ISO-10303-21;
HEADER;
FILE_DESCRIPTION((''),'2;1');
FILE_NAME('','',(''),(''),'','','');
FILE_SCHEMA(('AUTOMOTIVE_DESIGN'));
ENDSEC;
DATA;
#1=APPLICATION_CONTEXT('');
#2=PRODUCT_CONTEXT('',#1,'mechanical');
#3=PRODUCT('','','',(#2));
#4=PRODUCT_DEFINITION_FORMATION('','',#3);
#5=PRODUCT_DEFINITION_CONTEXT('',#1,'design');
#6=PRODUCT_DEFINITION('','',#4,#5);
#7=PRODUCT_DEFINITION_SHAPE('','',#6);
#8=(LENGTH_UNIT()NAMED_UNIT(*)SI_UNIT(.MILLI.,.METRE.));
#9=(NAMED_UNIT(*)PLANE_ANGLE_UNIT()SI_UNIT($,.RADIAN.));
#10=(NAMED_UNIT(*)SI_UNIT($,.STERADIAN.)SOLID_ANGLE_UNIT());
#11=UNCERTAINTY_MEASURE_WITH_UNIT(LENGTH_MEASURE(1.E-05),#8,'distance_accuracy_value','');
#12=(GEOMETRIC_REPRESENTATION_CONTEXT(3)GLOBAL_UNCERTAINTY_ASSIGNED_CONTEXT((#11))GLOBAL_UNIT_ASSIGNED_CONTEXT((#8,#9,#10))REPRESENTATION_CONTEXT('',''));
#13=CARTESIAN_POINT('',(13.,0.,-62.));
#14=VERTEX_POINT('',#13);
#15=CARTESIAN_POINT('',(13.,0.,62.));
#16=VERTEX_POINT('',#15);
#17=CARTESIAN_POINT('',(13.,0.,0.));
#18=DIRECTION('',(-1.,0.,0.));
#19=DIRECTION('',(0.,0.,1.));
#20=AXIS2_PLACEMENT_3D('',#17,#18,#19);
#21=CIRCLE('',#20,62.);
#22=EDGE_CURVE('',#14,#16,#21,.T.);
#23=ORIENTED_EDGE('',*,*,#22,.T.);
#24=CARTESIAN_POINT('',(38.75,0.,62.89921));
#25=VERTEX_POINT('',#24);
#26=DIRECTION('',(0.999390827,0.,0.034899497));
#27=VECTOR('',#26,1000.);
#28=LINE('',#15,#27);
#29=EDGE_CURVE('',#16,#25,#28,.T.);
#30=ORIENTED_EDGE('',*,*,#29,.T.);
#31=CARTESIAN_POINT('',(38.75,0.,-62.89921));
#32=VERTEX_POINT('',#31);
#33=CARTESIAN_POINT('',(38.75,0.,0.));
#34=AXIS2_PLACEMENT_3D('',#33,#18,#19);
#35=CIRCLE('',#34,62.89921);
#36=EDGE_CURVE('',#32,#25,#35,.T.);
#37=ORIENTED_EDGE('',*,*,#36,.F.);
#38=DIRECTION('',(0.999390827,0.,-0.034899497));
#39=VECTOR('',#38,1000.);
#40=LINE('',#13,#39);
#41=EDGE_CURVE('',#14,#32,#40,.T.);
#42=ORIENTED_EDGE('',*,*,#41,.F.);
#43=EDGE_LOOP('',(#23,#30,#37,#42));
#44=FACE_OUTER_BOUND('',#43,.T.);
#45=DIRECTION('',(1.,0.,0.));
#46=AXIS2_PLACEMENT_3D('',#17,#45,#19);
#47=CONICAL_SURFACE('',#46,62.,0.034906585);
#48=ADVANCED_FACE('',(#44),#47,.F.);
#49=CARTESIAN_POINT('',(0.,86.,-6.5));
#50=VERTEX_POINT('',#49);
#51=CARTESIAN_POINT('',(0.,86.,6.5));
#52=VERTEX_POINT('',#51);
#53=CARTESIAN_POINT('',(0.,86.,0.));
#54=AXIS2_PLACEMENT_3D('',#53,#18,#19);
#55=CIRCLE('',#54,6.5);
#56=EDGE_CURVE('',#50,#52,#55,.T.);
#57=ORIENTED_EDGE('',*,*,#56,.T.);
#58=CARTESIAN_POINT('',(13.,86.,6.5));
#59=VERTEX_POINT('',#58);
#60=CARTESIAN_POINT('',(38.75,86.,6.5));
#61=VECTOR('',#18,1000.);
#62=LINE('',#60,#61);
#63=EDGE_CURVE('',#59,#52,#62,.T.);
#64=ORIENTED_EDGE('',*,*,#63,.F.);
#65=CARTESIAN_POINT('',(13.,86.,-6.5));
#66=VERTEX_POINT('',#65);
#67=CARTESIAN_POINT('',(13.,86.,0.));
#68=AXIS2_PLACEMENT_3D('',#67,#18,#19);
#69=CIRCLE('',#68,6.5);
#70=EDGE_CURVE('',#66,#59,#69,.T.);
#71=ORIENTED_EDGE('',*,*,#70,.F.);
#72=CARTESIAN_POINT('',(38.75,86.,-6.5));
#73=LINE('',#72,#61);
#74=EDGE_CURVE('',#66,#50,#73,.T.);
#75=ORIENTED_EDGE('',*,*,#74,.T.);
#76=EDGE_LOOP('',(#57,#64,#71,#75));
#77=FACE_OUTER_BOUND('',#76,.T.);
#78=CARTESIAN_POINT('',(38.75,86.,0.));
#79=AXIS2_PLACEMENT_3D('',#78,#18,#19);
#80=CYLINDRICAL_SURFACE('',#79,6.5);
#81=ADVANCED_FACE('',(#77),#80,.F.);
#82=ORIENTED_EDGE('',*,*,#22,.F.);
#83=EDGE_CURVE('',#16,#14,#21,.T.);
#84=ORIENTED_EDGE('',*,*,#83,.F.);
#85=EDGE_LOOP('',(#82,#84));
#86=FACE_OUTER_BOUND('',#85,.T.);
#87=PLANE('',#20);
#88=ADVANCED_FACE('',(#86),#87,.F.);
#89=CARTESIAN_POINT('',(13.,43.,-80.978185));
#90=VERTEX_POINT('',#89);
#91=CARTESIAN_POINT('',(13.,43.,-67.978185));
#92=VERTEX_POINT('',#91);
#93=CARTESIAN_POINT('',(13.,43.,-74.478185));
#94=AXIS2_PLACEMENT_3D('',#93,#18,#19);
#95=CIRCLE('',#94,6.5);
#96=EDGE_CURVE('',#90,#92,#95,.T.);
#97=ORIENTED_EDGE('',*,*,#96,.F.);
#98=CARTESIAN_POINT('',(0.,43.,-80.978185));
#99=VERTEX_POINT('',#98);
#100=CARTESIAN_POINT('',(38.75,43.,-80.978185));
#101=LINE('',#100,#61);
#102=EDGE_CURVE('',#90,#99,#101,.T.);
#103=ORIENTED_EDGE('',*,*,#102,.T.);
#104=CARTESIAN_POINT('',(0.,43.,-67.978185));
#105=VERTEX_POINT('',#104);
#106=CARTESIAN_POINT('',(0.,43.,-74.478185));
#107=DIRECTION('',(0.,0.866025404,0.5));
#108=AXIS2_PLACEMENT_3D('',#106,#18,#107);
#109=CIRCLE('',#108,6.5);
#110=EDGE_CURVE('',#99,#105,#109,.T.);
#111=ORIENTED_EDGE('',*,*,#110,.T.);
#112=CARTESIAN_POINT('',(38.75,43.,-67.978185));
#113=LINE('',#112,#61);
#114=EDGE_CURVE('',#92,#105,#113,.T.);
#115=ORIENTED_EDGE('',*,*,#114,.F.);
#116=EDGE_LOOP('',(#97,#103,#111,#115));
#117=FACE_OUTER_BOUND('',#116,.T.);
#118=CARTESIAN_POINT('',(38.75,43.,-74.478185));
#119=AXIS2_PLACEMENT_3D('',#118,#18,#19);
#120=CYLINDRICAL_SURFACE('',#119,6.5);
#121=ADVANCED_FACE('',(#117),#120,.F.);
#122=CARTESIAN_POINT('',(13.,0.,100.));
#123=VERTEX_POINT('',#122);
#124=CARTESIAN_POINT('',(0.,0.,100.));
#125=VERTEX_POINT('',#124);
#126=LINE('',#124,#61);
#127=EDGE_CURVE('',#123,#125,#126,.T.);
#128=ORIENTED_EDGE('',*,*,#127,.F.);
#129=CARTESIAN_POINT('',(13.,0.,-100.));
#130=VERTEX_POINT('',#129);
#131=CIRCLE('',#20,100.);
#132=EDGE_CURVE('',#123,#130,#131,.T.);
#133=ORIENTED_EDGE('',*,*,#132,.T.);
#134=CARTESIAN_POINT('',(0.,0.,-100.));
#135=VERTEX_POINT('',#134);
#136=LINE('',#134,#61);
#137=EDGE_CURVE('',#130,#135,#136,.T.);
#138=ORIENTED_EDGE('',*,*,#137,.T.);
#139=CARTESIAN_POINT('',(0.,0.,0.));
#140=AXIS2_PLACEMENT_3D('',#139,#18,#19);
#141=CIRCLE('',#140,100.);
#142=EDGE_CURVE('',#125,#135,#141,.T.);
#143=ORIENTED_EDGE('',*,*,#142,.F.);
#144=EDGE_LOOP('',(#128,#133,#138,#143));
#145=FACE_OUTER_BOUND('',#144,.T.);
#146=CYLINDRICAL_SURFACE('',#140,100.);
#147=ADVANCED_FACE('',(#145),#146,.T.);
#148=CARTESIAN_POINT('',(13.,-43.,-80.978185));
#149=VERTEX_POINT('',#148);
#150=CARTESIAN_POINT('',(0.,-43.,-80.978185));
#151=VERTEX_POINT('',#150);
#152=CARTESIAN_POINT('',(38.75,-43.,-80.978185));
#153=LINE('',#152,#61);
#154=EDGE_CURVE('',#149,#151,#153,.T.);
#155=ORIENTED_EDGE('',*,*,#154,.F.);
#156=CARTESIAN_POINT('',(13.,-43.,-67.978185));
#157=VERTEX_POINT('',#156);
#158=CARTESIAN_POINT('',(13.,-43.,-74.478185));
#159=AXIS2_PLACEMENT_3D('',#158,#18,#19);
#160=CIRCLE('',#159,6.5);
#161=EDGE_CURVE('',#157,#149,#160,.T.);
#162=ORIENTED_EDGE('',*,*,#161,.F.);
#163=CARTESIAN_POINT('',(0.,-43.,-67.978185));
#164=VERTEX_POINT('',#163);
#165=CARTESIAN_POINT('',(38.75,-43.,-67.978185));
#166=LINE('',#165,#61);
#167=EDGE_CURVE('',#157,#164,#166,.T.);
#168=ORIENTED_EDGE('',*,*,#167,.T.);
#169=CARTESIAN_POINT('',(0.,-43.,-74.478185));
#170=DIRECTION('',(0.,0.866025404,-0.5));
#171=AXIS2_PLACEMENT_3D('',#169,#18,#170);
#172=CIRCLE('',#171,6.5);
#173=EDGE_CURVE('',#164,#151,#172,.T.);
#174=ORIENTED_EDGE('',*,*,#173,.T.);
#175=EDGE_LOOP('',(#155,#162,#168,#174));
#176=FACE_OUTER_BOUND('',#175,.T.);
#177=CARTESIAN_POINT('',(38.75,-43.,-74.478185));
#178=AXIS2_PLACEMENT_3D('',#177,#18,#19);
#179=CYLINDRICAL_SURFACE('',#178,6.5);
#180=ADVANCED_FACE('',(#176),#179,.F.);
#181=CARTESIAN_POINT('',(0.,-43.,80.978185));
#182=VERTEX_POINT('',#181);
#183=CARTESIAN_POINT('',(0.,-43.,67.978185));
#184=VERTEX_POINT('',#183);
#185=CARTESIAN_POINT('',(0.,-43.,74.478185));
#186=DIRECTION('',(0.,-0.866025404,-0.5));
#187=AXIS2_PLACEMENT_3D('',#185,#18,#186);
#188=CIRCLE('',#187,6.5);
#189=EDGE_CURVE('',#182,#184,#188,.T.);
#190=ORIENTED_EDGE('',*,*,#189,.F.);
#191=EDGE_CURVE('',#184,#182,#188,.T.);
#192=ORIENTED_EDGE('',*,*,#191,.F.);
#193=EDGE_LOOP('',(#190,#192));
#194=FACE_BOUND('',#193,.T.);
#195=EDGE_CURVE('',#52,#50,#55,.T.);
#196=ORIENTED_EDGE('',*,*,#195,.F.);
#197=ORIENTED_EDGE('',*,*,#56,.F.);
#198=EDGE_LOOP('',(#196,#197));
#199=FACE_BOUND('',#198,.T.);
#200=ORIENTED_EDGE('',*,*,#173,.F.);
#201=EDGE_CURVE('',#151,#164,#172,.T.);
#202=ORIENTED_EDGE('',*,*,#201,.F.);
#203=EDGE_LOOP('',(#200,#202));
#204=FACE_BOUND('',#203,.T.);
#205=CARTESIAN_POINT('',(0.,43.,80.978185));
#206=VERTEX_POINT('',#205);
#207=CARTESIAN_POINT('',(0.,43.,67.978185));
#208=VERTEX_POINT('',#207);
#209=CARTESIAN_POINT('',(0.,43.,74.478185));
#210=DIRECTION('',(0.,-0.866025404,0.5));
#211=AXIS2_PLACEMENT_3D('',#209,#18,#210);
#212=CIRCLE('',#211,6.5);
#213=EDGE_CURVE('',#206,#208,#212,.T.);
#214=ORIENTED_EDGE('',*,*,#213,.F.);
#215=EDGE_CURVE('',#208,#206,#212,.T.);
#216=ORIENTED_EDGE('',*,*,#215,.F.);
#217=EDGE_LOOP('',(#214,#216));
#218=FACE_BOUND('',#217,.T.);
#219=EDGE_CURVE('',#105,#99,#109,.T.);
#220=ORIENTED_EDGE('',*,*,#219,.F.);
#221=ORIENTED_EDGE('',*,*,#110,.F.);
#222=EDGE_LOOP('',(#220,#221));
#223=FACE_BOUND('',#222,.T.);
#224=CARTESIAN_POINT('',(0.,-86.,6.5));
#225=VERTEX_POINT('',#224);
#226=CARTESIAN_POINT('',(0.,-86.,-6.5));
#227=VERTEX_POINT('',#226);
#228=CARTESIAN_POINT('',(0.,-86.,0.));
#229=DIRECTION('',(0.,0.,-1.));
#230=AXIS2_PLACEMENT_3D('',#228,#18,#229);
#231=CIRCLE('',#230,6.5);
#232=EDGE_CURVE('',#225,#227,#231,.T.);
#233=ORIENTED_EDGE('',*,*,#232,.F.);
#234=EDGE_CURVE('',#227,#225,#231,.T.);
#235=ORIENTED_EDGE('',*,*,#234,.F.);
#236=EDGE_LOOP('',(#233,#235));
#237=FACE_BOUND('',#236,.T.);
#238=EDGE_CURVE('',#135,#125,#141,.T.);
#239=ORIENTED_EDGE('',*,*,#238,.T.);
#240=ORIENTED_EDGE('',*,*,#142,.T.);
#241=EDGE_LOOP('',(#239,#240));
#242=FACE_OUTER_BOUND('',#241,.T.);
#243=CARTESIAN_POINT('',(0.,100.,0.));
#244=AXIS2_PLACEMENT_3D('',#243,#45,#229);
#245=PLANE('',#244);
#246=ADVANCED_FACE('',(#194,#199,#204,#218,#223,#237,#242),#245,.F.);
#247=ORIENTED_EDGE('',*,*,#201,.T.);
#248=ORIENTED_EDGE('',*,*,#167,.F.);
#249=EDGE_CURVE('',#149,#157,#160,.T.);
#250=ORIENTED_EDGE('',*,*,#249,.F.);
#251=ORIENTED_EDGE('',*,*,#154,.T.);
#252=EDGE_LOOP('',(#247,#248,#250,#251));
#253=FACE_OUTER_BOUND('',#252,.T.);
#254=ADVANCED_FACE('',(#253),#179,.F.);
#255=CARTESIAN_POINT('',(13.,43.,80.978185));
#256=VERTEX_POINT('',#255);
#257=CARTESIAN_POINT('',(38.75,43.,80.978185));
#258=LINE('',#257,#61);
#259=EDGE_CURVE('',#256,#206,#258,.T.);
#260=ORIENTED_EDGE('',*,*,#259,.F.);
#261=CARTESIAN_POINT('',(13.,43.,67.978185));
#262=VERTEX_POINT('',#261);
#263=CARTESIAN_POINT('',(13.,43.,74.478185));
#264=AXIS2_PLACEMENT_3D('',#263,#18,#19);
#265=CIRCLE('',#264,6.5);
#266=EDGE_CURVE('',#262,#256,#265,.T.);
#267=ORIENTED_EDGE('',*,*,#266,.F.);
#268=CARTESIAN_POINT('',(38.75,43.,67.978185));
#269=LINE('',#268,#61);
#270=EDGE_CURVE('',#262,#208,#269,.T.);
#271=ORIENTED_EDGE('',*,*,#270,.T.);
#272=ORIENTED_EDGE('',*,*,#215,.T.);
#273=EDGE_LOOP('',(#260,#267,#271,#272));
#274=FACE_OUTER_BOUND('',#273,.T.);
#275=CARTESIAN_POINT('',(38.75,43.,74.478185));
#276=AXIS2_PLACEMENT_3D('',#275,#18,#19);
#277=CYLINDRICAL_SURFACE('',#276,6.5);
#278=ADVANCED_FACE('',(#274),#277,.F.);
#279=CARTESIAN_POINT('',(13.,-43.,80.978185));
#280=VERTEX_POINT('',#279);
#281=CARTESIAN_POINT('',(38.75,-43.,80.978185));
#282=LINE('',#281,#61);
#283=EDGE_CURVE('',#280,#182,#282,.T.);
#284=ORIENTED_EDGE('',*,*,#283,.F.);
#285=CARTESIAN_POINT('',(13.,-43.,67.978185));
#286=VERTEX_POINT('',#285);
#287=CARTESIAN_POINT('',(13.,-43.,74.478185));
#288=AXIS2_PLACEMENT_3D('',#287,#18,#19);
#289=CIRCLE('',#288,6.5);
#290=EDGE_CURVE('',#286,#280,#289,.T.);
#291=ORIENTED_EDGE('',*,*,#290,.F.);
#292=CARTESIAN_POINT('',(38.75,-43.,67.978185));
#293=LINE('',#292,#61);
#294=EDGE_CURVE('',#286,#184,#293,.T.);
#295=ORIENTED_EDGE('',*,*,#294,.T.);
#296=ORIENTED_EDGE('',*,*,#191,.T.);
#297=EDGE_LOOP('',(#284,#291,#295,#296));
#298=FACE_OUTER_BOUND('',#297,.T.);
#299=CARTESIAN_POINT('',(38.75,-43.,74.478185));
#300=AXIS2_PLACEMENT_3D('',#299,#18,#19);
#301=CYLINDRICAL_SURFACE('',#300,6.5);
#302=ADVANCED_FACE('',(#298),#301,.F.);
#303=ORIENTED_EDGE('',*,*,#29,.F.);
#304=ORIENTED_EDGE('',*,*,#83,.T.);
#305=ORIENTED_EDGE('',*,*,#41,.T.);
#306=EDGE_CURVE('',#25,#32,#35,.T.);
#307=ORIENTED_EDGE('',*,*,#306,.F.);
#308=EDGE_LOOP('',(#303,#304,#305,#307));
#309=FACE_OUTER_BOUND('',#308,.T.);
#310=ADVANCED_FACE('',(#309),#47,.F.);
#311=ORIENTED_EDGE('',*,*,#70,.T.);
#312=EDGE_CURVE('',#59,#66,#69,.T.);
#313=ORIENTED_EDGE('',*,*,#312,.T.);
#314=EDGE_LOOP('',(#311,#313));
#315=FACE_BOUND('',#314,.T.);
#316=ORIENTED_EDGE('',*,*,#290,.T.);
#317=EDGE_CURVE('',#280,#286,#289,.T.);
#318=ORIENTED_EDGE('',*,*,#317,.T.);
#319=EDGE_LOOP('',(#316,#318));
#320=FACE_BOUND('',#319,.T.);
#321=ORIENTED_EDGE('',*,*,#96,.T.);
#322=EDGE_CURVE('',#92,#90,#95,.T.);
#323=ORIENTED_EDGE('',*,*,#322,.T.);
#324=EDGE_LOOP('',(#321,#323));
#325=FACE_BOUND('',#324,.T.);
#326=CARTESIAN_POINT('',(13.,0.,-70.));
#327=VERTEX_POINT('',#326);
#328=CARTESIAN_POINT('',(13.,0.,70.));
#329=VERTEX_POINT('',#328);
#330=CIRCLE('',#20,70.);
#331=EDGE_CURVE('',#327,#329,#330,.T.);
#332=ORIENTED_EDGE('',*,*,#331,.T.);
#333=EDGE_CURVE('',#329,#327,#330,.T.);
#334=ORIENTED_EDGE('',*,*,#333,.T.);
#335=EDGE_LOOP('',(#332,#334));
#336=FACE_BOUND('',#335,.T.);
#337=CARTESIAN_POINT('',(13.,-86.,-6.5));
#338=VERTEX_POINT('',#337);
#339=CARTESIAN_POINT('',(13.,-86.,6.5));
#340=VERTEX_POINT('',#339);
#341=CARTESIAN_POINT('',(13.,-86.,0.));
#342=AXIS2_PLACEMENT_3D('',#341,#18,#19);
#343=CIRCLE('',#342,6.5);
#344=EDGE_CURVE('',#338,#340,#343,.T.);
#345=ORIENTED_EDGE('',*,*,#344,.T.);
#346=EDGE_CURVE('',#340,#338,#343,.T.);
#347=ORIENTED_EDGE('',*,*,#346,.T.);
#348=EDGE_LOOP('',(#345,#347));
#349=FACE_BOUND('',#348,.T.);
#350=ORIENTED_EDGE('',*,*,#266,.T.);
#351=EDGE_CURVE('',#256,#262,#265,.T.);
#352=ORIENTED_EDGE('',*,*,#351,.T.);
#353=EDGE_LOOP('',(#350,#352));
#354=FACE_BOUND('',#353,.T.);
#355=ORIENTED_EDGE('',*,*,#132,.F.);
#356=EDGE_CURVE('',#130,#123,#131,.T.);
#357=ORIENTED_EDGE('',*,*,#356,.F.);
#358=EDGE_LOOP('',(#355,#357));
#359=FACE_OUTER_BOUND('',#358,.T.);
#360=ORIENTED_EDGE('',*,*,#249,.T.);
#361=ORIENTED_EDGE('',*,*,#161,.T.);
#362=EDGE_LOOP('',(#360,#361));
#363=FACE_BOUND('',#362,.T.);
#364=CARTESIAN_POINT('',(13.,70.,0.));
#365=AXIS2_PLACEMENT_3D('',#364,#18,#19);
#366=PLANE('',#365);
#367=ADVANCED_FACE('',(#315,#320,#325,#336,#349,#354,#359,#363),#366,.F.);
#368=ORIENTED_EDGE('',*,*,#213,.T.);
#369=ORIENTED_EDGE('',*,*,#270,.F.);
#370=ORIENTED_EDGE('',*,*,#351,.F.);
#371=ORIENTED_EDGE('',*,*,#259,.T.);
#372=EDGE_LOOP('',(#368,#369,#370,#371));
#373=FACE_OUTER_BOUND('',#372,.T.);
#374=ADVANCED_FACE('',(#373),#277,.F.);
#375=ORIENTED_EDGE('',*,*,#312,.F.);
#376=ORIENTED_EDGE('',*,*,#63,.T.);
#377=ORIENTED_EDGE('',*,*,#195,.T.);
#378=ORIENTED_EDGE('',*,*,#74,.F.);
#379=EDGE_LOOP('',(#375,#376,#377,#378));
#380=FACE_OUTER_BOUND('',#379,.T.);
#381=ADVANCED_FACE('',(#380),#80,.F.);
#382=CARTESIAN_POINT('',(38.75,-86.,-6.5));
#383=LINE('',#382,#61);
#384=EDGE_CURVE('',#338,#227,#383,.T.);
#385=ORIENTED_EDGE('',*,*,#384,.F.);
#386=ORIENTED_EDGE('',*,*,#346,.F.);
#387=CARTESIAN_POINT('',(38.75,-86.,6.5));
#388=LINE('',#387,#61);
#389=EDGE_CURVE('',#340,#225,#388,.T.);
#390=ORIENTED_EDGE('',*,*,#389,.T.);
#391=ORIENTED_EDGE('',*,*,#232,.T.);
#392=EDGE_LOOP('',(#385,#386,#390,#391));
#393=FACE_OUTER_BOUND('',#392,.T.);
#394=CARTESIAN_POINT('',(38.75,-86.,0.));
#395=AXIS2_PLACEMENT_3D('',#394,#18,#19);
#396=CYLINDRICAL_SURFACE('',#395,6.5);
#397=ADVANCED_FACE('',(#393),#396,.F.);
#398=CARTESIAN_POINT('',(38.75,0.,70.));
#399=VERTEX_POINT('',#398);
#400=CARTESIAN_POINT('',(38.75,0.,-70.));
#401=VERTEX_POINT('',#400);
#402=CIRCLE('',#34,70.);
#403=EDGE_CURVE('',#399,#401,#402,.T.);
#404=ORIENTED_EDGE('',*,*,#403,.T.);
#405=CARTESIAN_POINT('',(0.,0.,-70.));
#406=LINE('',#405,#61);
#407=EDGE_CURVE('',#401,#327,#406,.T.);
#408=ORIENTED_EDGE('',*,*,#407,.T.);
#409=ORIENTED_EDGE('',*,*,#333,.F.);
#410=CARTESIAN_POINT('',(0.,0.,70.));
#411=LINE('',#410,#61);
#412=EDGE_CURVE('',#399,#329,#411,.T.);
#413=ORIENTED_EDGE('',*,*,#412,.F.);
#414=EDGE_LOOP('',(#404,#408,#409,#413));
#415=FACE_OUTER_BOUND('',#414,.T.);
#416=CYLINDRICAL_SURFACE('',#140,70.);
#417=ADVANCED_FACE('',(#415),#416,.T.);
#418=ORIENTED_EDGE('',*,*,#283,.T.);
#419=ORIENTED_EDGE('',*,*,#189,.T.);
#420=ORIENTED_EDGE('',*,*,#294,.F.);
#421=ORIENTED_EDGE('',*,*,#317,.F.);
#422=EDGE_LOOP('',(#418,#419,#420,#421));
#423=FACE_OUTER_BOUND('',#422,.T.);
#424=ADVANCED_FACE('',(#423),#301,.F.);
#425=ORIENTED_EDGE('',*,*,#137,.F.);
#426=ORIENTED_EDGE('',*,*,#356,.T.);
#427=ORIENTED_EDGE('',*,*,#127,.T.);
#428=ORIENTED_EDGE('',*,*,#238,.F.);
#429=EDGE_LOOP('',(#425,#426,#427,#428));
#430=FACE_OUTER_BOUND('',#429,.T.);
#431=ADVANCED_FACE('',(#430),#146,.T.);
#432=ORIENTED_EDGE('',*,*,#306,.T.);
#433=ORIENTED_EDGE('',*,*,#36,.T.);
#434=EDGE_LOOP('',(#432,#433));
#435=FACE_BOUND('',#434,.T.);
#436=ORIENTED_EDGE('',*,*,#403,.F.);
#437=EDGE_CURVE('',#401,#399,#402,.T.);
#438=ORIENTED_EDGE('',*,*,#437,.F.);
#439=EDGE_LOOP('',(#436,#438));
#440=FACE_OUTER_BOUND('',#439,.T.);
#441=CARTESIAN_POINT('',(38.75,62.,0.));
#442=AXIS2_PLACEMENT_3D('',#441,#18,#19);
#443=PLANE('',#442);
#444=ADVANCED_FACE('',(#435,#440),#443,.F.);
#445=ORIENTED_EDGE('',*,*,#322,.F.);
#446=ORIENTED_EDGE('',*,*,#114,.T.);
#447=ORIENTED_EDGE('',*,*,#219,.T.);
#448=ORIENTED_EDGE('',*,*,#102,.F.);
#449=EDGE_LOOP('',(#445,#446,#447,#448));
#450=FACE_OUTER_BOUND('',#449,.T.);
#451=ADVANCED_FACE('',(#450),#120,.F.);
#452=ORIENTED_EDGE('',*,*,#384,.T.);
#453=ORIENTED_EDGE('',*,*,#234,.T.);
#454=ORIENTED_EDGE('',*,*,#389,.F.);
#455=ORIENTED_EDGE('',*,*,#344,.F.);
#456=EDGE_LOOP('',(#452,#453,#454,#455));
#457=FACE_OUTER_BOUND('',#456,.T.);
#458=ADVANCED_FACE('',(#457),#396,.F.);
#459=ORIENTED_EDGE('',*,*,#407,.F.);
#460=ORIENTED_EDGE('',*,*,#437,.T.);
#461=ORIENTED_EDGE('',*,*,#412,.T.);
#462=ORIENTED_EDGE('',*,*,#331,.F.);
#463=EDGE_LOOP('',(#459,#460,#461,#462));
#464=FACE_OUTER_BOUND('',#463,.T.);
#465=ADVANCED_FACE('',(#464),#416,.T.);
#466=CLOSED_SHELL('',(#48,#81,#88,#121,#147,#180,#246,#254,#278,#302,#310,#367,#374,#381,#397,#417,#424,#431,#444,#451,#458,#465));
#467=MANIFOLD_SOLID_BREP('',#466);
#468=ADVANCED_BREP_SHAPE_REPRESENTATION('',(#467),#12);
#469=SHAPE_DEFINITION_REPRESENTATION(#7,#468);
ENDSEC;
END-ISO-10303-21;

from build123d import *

# Parameters (mm, degrees)
SKETCH2_R          = 6.5
CUT_EXTRUDE2_DEPTH = 147.63411097
CIRPATTERN1_COUNT  = 6
DRAFT1_ANGLE       = 2


with BuildPart() as part:
    # Sketch1 → Revolve1 (revolve)
    with BuildSketch(Plane.XY, mode=Mode.PRIVATE) as revolve1_sk:
        Polygon((0, 0), (13, 0), (13, 62), (38.75, 62), (38.75, 70), (13, 70), (13, 100), (0, 100), align=None)
    revolve(revolve1_sk.sketch.rotate(Axis((0, 0, 0), (1, 0, 0)), 90), axis=Axis((0, 0, 0), (1, 0, 0)))

    # Sketch2 → Cut-Extrude2 (cut, through all)
    with BuildSketch(Plane.ZY):
        with Locations((0, 86)):
            Circle(SKETCH2_R)
    cut_extrude2 = extrude(amount=-CUT_EXTRUDE2_DEPTH, mode=Mode.SUBTRACT)

    # CirPattern1: Cut-Extrude2 ×6 about axis
    cirpattern1_axis = Axis((0, 0, 0), (1, 0, 0))
    for i in range(1, CIRPATTERN1_COUNT):
        add(cut_extrude2.rotate(cirpattern1_axis, i * 360 / CIRPATTERN1_COUNT), mode=Mode.SUBTRACT)

    # Draft1
    draft1_faces = [part.faces().sort_by_distance(p)[0] for p in [
        (25.875, 0, -62),
    ]]
    draft(draft1_faces, Plane(origin=(13, 0, 0), x_dir=(0, 0, 1), z_dir=(1, 0, 0)), DRAFT1_ANGLE)


solid = part.part
